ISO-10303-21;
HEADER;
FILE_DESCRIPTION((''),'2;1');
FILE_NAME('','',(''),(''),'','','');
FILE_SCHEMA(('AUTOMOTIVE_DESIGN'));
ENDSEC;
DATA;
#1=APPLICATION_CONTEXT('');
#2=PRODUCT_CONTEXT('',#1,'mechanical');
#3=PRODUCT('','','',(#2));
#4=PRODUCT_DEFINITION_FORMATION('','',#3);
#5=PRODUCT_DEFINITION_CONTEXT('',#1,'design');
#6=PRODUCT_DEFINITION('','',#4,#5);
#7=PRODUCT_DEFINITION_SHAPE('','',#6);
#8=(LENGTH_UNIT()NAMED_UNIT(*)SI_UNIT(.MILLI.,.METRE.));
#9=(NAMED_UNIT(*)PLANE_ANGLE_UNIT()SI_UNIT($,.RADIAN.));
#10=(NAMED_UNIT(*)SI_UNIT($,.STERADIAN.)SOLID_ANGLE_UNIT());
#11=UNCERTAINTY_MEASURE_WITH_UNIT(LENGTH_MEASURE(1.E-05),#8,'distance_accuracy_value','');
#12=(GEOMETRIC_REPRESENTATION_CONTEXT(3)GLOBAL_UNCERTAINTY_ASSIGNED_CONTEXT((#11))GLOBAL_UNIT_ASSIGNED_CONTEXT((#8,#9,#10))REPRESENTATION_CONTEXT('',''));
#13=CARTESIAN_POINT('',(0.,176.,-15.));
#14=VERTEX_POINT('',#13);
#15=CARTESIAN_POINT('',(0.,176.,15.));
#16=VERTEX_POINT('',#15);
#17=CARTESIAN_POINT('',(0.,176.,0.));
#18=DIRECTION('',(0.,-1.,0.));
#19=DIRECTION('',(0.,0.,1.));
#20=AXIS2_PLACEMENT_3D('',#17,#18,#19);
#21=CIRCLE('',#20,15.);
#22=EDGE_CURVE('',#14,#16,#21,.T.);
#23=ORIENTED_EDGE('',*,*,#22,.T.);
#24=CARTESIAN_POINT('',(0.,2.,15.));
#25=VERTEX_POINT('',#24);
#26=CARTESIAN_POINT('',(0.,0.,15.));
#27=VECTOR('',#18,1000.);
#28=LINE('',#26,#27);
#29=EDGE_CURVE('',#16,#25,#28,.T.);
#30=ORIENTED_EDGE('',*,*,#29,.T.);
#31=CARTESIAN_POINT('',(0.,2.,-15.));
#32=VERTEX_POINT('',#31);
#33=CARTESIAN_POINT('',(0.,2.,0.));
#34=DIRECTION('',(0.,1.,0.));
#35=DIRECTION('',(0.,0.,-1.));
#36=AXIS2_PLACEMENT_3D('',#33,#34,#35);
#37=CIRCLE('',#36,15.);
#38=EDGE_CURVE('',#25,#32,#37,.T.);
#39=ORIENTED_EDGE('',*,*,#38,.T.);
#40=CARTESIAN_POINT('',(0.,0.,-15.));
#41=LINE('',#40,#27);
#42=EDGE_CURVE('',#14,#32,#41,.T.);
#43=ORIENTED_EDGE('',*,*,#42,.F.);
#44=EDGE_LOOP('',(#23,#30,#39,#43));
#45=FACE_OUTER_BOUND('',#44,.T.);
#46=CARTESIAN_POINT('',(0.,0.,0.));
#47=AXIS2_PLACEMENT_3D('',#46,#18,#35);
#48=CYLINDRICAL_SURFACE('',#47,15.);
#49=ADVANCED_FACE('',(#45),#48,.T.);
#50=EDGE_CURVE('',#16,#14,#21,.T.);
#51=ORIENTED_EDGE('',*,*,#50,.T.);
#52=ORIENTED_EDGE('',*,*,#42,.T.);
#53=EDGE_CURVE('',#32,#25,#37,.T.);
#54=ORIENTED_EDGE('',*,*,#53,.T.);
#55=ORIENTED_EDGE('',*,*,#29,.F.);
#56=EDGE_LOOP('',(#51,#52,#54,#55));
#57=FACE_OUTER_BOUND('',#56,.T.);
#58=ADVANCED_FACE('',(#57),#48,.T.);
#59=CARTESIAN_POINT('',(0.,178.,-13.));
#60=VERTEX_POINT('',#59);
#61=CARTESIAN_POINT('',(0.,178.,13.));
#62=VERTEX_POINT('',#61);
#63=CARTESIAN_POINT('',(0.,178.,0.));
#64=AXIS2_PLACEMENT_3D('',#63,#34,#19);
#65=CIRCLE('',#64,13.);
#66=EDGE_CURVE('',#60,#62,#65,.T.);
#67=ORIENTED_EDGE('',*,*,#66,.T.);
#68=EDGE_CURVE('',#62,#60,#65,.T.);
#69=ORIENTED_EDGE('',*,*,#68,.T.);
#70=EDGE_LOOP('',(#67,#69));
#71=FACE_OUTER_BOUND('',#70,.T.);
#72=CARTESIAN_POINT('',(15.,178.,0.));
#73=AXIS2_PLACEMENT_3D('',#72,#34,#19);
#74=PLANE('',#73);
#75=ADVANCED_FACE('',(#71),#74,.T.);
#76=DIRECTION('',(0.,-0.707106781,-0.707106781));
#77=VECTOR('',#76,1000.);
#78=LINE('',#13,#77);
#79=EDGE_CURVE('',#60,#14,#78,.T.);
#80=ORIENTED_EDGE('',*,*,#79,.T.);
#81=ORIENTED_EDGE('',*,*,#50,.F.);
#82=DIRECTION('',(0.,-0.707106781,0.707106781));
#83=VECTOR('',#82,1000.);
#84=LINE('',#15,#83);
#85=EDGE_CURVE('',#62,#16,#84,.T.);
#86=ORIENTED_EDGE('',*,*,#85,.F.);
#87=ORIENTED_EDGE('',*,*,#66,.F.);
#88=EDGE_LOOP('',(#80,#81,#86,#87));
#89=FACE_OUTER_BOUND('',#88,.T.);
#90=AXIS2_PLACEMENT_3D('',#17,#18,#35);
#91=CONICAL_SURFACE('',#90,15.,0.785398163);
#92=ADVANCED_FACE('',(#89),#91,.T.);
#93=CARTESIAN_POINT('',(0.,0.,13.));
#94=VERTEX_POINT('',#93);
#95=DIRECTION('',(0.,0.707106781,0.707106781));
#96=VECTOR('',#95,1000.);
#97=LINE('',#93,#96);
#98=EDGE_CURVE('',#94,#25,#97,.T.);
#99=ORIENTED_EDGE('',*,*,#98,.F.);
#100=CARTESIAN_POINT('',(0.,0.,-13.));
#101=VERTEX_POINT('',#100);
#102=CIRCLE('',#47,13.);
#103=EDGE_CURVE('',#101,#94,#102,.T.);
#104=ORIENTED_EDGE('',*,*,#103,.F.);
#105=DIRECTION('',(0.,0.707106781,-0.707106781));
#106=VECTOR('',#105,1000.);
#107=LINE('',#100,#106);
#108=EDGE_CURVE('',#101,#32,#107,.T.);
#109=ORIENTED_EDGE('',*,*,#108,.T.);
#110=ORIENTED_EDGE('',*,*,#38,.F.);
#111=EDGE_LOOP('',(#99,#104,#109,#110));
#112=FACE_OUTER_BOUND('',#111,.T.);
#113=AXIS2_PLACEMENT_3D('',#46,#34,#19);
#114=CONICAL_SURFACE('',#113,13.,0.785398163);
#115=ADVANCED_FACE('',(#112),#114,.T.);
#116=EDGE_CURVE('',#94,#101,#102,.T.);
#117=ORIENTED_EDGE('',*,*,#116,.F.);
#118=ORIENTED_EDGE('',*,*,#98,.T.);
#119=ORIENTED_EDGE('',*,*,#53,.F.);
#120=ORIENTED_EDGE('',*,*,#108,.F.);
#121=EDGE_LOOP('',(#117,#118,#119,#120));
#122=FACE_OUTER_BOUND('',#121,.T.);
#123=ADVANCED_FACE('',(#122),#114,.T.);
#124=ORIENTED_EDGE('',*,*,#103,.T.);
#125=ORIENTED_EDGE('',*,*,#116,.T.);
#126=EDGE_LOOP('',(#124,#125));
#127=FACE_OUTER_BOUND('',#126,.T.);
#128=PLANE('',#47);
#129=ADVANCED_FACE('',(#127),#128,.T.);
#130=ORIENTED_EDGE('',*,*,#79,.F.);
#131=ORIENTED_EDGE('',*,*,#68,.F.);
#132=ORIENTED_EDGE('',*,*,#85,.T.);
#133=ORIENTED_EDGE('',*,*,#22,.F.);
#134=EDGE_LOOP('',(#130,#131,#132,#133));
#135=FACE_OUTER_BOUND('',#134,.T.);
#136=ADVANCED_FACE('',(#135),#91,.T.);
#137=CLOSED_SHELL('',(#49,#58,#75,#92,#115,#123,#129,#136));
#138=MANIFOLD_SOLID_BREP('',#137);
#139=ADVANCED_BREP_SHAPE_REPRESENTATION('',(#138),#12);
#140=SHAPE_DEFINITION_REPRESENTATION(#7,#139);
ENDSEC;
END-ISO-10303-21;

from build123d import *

# Parameters (mm, degrees)
SKETCH1_W     = 15
SKETCH1_H     = 178
CHAMFER1_SIZE = 2


with BuildPart() as part:
    # Sketch1 → Revolve1 (revolve)
    with BuildSketch(Plane.XY, mode=Mode.PRIVATE) as revolve1_sk:
        with Locations((7.5, 89)):
            Rectangle(SKETCH1_W, SKETCH1_H)
    revolve(revolve1_sk.sketch.rotate(Axis((0, 0, 0), (0, 1, 0)), 90), axis=Axis((0, 0, 0), (0, 1, 0)))

    # Chamfer1
    chamfer1_edges = [part.edges().sort_by_distance(p)[0] for p in [
        (0, 178, 15),
        (0, 0, 15),
    ]]
    chamfer(chamfer1_edges, length=CHAMFER1_SIZE)


solid = part.part
